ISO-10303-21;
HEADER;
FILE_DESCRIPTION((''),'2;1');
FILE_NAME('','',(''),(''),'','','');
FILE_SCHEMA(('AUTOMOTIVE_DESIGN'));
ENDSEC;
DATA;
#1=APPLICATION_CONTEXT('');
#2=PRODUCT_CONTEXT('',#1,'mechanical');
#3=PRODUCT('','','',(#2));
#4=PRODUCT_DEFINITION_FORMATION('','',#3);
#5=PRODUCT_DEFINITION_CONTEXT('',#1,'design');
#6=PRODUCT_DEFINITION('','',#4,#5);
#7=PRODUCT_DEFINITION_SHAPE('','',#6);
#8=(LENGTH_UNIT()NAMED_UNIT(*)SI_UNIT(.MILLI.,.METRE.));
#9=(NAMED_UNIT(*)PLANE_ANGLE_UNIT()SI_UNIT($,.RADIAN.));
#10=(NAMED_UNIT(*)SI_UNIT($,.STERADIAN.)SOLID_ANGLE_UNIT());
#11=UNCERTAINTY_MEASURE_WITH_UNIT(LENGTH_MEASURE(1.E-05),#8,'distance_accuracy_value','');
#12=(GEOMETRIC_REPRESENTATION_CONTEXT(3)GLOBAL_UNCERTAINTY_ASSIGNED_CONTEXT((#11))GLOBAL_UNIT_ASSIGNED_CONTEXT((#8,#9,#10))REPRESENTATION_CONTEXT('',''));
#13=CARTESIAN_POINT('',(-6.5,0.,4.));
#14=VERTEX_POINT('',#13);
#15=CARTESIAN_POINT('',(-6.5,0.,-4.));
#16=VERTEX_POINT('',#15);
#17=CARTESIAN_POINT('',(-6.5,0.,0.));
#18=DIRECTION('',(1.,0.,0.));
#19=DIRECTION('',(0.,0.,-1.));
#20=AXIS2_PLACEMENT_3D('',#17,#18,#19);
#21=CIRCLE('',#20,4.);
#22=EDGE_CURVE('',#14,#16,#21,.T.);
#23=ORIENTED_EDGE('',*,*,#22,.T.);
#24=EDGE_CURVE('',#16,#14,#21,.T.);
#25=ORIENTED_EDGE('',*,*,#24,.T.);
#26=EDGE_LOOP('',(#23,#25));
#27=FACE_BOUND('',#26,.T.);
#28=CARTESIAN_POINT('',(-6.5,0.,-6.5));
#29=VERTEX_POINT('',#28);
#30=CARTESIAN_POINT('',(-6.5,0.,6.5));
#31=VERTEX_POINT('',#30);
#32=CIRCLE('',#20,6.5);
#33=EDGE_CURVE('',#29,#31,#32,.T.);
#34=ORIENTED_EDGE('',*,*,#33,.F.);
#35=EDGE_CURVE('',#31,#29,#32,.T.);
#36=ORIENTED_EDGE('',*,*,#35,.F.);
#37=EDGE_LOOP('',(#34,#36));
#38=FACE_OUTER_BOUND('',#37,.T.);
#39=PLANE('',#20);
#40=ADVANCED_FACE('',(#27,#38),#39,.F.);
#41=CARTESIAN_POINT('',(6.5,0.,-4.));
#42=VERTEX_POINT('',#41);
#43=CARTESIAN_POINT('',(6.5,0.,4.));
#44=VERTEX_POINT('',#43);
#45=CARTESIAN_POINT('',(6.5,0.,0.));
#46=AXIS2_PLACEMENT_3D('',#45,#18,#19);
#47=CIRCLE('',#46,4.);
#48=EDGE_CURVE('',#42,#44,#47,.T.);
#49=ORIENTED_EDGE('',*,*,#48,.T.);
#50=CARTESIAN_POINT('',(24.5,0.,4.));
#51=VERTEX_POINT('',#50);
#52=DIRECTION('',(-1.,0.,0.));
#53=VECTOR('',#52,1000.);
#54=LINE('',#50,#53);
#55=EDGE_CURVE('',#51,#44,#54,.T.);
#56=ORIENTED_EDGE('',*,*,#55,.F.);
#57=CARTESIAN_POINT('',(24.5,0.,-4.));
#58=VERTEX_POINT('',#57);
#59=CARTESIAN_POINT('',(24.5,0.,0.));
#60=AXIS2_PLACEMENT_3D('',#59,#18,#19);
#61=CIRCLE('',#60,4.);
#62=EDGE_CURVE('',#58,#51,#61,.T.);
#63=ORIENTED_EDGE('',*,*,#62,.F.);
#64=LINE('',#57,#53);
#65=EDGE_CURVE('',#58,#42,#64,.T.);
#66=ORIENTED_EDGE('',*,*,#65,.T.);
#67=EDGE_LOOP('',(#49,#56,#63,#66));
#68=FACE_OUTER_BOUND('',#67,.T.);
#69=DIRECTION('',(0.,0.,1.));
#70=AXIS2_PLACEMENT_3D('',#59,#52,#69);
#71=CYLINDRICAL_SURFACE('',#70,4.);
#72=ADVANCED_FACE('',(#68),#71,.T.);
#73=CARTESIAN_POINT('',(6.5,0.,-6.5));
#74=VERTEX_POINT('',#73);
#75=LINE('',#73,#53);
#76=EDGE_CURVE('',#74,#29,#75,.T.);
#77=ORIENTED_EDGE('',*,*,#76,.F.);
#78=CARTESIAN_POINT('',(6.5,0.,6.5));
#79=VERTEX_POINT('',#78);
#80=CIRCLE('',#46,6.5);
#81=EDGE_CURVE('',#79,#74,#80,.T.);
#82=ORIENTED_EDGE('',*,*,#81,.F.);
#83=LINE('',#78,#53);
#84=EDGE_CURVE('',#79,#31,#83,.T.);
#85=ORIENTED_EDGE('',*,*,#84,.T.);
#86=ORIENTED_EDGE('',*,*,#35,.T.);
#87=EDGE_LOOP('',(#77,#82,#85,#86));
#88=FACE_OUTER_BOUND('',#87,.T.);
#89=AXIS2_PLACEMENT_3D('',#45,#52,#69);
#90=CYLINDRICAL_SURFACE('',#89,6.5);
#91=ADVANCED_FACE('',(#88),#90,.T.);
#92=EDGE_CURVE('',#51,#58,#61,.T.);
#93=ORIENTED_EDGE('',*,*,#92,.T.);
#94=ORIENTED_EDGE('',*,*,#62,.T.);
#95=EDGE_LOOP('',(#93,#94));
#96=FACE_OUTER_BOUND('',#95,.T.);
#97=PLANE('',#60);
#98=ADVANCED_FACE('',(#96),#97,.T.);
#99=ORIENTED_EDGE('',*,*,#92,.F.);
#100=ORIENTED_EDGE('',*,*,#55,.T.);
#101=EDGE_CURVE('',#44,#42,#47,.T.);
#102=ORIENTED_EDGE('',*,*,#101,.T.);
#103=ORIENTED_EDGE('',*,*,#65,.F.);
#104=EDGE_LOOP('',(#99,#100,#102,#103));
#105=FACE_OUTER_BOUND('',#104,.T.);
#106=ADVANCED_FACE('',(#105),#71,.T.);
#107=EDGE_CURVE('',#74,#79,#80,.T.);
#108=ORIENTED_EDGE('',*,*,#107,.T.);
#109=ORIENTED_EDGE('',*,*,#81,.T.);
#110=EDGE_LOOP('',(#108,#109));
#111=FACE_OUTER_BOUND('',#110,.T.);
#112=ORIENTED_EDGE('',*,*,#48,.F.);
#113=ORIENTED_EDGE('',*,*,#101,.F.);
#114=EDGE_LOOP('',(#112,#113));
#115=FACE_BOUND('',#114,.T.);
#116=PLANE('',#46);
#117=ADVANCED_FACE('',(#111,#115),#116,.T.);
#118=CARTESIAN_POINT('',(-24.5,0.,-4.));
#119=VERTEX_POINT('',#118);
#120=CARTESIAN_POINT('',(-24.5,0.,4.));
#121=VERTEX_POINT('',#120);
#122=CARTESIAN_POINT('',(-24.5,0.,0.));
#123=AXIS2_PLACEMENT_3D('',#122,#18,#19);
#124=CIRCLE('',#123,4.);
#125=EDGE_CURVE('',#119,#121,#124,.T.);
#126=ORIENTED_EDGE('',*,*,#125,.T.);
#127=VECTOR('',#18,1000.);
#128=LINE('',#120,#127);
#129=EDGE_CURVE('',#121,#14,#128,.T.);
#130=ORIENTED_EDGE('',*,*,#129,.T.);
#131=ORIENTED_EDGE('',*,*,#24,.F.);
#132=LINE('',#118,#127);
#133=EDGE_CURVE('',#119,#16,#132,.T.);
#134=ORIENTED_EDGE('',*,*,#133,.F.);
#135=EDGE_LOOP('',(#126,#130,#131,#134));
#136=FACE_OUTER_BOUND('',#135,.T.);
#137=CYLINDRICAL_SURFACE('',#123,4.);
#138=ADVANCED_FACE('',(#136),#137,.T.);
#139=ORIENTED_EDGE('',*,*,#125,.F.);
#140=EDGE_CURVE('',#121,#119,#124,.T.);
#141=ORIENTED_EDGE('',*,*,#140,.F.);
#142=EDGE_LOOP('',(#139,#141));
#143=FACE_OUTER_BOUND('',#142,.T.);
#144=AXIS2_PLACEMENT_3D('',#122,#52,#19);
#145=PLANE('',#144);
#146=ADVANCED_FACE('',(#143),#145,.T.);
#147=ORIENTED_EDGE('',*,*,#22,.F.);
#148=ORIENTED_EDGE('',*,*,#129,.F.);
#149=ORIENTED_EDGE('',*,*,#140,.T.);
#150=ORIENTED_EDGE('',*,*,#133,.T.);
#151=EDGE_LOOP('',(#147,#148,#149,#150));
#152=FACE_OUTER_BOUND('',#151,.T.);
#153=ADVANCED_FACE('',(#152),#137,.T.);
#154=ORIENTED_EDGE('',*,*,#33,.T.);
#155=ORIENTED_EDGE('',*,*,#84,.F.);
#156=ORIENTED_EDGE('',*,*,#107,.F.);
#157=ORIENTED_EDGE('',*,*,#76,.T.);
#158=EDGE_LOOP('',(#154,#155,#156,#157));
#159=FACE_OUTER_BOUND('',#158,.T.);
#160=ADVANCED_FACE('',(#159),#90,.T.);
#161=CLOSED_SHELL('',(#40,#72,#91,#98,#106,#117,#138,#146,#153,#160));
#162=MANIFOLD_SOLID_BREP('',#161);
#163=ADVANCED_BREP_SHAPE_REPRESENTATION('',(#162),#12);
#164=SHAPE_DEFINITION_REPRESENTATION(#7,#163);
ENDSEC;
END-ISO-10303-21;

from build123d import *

# Parameters (mm, degrees)
SKETCH1_R           = 6.5
BOSS_EXTRUDE1_DEPTH = 6.5
SKETCH3_R           = 4
BOSS_EXTRUDE2_DEPTH = 18


with BuildPart() as part:
    # Sketch1 → Boss-Extrude1 (new, symmetric)
    with BuildSketch(Plane(origin=(0, 0, 0), x_dir=(0, 0, -1), z_dir=(1, 0, 0))):
        with Locations(Location((0, 0, 0), (0, 0, 180))):
            Circle(SKETCH1_R)
    extrude(amount=BOSS_EXTRUDE1_DEPTH, both=True)

    # Sketch3 → Boss-Extrude2 (add)
    with BuildSketch(Plane(origin=(6.5, 0, 0), x_dir=(0, 0, -1), z_dir=(1, 0, 0))):
        Circle(SKETCH3_R)
    boss_extrude2 = extrude(amount=BOSS_EXTRUDE2_DEPTH)

    # Mirror1: Boss-Extrude2 across plane
    add(boss_extrude2.mirror(Plane(origin=(0, 0, 0), x_dir=(0, 0, 1), z_dir=(1, 0, 0))))


solid = part.part
